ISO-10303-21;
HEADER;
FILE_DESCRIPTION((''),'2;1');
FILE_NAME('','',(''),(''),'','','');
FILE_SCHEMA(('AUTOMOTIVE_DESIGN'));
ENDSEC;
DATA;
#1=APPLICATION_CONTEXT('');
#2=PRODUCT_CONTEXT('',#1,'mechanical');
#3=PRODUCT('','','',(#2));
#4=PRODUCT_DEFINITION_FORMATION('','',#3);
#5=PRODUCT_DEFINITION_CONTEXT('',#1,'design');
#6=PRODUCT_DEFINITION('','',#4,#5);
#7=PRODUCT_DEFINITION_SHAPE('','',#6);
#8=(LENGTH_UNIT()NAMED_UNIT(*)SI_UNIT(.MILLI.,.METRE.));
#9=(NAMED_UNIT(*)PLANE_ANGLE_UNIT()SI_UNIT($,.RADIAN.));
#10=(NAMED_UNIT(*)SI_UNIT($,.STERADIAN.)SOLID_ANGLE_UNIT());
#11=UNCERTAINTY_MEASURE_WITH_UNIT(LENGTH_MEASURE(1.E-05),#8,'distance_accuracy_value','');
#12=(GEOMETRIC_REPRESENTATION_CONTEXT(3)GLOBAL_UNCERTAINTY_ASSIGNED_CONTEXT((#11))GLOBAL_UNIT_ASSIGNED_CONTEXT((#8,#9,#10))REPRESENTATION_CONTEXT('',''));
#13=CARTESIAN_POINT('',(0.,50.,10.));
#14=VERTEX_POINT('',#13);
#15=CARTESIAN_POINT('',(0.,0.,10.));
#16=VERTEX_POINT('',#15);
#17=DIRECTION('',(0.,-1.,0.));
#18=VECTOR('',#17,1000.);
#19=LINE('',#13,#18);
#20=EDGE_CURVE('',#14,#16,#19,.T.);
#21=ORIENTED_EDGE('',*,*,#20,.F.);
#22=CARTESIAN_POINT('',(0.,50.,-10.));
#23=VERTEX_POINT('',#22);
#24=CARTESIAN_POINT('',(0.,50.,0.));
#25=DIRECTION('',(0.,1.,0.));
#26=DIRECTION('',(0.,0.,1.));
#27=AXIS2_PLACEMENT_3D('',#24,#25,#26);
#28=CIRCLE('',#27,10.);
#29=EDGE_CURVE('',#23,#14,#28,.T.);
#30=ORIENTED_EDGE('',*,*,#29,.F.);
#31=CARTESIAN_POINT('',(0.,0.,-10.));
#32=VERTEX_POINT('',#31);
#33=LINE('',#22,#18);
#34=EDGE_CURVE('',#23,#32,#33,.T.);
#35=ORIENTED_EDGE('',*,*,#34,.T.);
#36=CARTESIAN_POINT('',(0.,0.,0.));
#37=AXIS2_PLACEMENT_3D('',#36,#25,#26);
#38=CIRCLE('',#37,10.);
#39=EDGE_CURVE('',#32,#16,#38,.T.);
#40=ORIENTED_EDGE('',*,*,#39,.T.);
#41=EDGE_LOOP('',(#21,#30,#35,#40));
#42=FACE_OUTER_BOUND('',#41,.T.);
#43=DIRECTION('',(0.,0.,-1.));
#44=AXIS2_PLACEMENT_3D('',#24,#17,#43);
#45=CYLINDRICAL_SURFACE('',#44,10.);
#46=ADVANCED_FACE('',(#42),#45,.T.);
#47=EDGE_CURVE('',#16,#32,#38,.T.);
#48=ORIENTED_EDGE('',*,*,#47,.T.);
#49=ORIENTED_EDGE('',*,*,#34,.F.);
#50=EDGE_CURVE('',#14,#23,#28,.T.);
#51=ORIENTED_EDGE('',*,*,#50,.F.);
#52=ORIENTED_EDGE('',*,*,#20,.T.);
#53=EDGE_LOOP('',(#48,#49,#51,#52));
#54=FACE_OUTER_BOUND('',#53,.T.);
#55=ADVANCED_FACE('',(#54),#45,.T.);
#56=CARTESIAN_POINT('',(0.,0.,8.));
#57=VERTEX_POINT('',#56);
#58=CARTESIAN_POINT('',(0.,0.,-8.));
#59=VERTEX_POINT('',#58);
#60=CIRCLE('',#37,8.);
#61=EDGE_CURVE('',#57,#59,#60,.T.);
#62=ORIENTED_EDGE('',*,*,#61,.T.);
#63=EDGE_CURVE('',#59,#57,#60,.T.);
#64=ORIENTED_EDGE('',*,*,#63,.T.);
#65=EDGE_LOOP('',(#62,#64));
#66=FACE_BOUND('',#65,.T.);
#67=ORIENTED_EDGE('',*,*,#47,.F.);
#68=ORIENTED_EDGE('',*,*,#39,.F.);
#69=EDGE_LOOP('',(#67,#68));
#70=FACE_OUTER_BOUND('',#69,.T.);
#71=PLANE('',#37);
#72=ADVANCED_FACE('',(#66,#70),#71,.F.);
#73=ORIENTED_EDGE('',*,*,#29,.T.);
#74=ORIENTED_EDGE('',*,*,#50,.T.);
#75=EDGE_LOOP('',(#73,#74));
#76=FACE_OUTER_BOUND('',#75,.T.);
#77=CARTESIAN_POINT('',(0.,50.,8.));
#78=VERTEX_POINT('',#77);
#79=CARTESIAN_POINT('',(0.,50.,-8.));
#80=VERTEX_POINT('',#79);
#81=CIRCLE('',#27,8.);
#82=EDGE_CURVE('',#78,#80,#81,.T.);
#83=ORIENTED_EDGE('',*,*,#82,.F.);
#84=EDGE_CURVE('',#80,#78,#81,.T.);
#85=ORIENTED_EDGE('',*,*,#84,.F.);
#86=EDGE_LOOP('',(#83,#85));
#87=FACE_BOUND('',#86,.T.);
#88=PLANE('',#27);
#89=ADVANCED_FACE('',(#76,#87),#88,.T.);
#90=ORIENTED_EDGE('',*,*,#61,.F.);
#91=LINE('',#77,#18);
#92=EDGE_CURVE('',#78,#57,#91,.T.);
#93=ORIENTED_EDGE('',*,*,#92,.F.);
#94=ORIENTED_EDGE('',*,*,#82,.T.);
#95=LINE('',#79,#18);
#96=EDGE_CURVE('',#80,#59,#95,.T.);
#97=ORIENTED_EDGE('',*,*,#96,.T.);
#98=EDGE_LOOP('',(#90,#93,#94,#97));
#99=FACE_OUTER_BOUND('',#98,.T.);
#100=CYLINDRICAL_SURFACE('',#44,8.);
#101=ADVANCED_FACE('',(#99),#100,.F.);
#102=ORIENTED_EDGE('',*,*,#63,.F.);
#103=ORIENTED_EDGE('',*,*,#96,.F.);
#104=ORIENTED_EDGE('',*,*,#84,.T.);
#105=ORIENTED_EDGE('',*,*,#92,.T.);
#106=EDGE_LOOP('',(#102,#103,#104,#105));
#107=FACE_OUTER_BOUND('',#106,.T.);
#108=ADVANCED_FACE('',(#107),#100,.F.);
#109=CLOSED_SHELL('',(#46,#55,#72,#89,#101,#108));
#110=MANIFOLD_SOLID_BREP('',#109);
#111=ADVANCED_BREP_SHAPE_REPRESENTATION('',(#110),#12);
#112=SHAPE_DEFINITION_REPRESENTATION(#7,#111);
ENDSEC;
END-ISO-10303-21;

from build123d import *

# Parameters (mm, degrees)
SKETCH1_R           = 10
SKETCH1_R_2         = 8
BOSS_EXTRUDE1_DEPTH = 50


with BuildPart() as part:
    # Sketch1 → Boss-Extrude1 (new body)
    with BuildSketch(Plane(origin=(0, 0, 0), x_dir=(1, 0, 0), z_dir=(0, 1, 0))):
        with Locations(Location((0, 0, 0), (0, 0, 270))):
            Circle(SKETCH1_R)
        with Locations(Location((0, 0, 0), (0, 0, 270))):
            Circle(SKETCH1_R_2, mode=Mode.SUBTRACT)
    extrude(amount=BOSS_EXTRUDE1_DEPTH)


solid = part.part
